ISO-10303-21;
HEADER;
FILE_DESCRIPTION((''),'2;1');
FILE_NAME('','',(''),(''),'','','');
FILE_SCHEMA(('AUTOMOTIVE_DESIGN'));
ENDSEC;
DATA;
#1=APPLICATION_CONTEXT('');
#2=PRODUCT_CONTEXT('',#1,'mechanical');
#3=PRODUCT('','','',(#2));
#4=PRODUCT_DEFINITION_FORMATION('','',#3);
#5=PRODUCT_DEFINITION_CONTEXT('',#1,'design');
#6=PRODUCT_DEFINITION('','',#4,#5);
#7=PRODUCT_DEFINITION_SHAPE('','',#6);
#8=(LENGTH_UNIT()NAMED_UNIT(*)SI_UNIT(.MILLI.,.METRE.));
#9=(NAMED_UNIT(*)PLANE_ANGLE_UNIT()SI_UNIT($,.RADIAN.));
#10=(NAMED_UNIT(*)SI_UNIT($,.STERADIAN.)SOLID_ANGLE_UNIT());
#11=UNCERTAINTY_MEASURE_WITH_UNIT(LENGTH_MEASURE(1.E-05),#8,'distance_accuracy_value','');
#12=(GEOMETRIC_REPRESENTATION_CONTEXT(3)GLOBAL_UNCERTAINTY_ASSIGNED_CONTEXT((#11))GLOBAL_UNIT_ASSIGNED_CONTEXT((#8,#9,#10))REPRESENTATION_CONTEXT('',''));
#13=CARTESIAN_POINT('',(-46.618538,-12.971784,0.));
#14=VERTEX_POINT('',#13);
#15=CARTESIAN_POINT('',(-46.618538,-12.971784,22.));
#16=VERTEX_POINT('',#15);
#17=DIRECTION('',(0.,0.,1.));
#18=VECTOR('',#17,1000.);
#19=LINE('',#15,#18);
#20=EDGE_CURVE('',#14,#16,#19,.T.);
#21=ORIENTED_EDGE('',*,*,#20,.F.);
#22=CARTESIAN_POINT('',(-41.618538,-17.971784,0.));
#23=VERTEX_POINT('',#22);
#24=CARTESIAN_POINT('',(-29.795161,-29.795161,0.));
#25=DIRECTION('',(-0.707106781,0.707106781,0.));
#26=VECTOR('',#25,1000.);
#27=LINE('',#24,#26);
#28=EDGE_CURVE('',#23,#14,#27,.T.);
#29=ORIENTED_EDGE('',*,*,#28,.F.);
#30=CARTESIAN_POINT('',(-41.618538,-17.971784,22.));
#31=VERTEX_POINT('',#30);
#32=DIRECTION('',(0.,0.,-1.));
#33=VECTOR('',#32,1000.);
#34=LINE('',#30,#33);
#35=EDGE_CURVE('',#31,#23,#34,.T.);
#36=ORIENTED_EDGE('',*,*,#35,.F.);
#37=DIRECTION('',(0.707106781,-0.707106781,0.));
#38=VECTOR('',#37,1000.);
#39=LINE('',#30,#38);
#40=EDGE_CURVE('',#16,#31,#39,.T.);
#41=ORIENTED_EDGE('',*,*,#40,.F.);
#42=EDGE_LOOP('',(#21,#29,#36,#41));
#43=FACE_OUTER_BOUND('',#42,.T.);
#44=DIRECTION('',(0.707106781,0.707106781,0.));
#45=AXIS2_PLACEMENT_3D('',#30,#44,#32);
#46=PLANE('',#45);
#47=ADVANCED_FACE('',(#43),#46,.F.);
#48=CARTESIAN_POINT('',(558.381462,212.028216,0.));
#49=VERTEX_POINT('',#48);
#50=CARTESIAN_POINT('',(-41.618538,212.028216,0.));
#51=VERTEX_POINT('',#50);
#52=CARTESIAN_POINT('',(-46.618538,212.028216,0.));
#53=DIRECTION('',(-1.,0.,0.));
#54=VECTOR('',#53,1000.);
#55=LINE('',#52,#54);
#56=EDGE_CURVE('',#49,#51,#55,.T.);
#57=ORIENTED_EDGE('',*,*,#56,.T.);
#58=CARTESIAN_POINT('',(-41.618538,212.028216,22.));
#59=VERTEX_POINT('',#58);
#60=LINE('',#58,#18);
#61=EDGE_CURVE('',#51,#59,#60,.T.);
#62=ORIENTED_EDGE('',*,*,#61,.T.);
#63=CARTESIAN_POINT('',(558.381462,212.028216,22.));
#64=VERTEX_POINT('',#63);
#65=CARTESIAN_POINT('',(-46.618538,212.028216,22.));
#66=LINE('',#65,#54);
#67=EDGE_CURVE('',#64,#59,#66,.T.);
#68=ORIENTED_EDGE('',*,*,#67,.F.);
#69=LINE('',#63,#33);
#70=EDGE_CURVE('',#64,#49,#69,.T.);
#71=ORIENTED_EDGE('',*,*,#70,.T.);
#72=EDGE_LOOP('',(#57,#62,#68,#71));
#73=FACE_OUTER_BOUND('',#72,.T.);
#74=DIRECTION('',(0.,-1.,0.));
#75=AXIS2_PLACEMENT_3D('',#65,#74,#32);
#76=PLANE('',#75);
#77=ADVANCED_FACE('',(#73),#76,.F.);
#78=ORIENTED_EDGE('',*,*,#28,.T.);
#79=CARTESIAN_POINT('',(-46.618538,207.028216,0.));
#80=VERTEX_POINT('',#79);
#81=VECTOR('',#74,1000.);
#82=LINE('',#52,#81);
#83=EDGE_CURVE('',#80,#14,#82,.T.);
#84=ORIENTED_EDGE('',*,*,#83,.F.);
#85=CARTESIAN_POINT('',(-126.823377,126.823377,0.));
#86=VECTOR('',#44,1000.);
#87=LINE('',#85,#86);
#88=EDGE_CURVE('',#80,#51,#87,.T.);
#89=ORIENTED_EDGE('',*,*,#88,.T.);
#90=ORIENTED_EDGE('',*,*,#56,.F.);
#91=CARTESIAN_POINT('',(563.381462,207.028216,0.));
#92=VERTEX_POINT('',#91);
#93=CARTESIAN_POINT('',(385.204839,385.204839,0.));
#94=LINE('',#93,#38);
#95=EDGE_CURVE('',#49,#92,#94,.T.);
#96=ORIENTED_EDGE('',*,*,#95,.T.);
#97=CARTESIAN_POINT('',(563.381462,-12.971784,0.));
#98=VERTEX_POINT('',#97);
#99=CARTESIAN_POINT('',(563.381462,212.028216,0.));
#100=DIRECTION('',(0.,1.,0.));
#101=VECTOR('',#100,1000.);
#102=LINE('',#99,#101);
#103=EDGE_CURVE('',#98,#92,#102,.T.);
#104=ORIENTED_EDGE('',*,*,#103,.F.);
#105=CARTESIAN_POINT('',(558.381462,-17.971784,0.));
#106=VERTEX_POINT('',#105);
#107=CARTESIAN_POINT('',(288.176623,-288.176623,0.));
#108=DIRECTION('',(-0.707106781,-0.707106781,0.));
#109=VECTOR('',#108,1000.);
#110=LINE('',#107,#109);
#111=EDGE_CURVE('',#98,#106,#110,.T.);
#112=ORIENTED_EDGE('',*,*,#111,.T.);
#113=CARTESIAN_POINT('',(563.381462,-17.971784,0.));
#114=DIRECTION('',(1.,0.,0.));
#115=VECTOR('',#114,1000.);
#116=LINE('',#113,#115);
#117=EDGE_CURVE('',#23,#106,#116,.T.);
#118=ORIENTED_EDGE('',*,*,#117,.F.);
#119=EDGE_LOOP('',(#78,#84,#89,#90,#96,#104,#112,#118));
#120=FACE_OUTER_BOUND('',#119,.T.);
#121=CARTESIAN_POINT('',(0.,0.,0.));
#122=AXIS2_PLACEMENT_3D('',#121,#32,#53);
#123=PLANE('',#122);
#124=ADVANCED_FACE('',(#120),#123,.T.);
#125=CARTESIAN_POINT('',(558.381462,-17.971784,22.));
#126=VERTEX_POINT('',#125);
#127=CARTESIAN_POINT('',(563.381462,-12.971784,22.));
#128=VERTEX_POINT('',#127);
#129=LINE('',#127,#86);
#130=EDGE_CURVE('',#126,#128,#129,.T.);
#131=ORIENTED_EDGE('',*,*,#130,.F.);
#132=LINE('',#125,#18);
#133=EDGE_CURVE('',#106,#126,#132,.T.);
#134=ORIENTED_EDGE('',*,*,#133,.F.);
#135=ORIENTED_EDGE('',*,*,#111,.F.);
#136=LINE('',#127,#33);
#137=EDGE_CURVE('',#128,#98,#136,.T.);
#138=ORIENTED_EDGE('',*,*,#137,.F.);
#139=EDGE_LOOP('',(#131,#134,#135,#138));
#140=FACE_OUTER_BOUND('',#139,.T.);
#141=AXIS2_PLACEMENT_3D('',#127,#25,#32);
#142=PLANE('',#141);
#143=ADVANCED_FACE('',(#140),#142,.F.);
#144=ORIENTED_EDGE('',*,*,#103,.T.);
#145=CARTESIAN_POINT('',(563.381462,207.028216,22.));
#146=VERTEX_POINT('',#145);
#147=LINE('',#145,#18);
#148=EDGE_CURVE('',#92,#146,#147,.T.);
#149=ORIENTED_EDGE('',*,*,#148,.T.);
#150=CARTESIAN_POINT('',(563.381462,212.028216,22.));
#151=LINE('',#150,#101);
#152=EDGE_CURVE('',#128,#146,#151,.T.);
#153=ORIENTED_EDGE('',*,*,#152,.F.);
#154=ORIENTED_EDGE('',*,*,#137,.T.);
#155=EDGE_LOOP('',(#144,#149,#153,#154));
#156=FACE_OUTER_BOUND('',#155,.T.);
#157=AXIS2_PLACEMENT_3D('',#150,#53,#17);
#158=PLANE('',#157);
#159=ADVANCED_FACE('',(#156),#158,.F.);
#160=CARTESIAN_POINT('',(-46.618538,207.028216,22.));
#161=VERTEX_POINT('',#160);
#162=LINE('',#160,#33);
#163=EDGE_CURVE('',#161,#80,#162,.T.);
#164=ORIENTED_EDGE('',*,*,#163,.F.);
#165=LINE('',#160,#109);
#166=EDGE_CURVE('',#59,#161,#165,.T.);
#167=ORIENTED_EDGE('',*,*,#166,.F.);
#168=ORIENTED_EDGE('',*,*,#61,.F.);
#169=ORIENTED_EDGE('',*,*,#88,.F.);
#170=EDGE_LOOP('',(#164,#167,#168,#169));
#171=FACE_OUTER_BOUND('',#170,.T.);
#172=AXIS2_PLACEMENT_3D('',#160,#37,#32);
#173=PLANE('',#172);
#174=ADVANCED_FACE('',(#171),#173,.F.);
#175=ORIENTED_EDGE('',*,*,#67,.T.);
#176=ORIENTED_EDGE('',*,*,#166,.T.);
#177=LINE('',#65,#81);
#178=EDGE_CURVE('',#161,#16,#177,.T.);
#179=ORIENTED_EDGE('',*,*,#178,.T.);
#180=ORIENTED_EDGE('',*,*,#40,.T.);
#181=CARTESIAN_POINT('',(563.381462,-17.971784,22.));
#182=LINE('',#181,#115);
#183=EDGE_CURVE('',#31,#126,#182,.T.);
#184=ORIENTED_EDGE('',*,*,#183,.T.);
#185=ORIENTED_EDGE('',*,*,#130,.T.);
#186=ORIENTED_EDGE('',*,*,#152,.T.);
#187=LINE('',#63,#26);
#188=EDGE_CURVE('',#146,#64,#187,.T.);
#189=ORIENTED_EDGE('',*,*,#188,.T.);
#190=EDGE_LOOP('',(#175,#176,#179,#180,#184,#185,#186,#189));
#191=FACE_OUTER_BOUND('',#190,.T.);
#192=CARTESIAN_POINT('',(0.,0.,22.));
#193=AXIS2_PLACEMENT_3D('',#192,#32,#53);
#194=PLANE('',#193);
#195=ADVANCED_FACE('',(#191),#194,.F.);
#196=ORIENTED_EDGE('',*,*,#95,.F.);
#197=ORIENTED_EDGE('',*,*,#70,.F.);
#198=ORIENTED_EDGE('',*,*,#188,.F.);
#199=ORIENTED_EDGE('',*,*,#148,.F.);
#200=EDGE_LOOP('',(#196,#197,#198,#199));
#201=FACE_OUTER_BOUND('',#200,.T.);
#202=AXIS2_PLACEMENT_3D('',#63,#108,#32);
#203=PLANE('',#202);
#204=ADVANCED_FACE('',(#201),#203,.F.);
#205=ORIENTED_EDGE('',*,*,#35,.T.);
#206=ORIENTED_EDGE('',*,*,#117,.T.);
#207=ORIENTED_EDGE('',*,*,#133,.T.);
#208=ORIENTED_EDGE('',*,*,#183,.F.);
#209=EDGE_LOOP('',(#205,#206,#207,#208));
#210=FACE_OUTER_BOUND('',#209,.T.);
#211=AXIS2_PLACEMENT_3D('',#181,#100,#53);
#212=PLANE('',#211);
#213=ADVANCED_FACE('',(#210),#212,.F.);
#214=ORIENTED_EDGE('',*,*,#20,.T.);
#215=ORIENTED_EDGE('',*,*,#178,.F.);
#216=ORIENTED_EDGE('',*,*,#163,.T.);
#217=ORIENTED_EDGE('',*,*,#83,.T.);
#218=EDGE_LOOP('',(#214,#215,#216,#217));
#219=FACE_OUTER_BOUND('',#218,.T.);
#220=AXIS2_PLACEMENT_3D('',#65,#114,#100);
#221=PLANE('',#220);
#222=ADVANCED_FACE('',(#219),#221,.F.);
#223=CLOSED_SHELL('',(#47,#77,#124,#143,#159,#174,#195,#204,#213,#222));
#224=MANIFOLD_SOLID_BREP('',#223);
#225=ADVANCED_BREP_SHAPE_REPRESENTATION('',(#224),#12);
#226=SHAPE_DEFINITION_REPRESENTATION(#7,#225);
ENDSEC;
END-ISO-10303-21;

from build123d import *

# Parameters (mm, degrees)
SKETCH1_W           = 610
SKETCH1_H           = 230
BOSS_EXTRUDE1_DEPTH = 22
CHAMFER1_SIZE       = 5


with BuildPart() as part:
    # Sketch1 → Boss-Extrude1 (new body)
    with BuildSketch(Plane.XY):
        with Locations((258.381462009, 97.028215789)):
            Rectangle(SKETCH1_W, SKETCH1_H)
    extrude(amount=BOSS_EXTRUDE1_DEPTH)

    # Chamfer1
    chamfer1_edges = [part.edges().sort_by_distance(p)[0] for p in [
        (563.381462009, 212.028215789, 11),
        (563.381462009, -17.971784211, 11),
        (-46.618537991, -17.971784211, 11),
        (-46.618537991, 212.028215789, 11),
    ]]
    chamfer(chamfer1_edges, length=CHAMFER1_SIZE)


solid = part.part
